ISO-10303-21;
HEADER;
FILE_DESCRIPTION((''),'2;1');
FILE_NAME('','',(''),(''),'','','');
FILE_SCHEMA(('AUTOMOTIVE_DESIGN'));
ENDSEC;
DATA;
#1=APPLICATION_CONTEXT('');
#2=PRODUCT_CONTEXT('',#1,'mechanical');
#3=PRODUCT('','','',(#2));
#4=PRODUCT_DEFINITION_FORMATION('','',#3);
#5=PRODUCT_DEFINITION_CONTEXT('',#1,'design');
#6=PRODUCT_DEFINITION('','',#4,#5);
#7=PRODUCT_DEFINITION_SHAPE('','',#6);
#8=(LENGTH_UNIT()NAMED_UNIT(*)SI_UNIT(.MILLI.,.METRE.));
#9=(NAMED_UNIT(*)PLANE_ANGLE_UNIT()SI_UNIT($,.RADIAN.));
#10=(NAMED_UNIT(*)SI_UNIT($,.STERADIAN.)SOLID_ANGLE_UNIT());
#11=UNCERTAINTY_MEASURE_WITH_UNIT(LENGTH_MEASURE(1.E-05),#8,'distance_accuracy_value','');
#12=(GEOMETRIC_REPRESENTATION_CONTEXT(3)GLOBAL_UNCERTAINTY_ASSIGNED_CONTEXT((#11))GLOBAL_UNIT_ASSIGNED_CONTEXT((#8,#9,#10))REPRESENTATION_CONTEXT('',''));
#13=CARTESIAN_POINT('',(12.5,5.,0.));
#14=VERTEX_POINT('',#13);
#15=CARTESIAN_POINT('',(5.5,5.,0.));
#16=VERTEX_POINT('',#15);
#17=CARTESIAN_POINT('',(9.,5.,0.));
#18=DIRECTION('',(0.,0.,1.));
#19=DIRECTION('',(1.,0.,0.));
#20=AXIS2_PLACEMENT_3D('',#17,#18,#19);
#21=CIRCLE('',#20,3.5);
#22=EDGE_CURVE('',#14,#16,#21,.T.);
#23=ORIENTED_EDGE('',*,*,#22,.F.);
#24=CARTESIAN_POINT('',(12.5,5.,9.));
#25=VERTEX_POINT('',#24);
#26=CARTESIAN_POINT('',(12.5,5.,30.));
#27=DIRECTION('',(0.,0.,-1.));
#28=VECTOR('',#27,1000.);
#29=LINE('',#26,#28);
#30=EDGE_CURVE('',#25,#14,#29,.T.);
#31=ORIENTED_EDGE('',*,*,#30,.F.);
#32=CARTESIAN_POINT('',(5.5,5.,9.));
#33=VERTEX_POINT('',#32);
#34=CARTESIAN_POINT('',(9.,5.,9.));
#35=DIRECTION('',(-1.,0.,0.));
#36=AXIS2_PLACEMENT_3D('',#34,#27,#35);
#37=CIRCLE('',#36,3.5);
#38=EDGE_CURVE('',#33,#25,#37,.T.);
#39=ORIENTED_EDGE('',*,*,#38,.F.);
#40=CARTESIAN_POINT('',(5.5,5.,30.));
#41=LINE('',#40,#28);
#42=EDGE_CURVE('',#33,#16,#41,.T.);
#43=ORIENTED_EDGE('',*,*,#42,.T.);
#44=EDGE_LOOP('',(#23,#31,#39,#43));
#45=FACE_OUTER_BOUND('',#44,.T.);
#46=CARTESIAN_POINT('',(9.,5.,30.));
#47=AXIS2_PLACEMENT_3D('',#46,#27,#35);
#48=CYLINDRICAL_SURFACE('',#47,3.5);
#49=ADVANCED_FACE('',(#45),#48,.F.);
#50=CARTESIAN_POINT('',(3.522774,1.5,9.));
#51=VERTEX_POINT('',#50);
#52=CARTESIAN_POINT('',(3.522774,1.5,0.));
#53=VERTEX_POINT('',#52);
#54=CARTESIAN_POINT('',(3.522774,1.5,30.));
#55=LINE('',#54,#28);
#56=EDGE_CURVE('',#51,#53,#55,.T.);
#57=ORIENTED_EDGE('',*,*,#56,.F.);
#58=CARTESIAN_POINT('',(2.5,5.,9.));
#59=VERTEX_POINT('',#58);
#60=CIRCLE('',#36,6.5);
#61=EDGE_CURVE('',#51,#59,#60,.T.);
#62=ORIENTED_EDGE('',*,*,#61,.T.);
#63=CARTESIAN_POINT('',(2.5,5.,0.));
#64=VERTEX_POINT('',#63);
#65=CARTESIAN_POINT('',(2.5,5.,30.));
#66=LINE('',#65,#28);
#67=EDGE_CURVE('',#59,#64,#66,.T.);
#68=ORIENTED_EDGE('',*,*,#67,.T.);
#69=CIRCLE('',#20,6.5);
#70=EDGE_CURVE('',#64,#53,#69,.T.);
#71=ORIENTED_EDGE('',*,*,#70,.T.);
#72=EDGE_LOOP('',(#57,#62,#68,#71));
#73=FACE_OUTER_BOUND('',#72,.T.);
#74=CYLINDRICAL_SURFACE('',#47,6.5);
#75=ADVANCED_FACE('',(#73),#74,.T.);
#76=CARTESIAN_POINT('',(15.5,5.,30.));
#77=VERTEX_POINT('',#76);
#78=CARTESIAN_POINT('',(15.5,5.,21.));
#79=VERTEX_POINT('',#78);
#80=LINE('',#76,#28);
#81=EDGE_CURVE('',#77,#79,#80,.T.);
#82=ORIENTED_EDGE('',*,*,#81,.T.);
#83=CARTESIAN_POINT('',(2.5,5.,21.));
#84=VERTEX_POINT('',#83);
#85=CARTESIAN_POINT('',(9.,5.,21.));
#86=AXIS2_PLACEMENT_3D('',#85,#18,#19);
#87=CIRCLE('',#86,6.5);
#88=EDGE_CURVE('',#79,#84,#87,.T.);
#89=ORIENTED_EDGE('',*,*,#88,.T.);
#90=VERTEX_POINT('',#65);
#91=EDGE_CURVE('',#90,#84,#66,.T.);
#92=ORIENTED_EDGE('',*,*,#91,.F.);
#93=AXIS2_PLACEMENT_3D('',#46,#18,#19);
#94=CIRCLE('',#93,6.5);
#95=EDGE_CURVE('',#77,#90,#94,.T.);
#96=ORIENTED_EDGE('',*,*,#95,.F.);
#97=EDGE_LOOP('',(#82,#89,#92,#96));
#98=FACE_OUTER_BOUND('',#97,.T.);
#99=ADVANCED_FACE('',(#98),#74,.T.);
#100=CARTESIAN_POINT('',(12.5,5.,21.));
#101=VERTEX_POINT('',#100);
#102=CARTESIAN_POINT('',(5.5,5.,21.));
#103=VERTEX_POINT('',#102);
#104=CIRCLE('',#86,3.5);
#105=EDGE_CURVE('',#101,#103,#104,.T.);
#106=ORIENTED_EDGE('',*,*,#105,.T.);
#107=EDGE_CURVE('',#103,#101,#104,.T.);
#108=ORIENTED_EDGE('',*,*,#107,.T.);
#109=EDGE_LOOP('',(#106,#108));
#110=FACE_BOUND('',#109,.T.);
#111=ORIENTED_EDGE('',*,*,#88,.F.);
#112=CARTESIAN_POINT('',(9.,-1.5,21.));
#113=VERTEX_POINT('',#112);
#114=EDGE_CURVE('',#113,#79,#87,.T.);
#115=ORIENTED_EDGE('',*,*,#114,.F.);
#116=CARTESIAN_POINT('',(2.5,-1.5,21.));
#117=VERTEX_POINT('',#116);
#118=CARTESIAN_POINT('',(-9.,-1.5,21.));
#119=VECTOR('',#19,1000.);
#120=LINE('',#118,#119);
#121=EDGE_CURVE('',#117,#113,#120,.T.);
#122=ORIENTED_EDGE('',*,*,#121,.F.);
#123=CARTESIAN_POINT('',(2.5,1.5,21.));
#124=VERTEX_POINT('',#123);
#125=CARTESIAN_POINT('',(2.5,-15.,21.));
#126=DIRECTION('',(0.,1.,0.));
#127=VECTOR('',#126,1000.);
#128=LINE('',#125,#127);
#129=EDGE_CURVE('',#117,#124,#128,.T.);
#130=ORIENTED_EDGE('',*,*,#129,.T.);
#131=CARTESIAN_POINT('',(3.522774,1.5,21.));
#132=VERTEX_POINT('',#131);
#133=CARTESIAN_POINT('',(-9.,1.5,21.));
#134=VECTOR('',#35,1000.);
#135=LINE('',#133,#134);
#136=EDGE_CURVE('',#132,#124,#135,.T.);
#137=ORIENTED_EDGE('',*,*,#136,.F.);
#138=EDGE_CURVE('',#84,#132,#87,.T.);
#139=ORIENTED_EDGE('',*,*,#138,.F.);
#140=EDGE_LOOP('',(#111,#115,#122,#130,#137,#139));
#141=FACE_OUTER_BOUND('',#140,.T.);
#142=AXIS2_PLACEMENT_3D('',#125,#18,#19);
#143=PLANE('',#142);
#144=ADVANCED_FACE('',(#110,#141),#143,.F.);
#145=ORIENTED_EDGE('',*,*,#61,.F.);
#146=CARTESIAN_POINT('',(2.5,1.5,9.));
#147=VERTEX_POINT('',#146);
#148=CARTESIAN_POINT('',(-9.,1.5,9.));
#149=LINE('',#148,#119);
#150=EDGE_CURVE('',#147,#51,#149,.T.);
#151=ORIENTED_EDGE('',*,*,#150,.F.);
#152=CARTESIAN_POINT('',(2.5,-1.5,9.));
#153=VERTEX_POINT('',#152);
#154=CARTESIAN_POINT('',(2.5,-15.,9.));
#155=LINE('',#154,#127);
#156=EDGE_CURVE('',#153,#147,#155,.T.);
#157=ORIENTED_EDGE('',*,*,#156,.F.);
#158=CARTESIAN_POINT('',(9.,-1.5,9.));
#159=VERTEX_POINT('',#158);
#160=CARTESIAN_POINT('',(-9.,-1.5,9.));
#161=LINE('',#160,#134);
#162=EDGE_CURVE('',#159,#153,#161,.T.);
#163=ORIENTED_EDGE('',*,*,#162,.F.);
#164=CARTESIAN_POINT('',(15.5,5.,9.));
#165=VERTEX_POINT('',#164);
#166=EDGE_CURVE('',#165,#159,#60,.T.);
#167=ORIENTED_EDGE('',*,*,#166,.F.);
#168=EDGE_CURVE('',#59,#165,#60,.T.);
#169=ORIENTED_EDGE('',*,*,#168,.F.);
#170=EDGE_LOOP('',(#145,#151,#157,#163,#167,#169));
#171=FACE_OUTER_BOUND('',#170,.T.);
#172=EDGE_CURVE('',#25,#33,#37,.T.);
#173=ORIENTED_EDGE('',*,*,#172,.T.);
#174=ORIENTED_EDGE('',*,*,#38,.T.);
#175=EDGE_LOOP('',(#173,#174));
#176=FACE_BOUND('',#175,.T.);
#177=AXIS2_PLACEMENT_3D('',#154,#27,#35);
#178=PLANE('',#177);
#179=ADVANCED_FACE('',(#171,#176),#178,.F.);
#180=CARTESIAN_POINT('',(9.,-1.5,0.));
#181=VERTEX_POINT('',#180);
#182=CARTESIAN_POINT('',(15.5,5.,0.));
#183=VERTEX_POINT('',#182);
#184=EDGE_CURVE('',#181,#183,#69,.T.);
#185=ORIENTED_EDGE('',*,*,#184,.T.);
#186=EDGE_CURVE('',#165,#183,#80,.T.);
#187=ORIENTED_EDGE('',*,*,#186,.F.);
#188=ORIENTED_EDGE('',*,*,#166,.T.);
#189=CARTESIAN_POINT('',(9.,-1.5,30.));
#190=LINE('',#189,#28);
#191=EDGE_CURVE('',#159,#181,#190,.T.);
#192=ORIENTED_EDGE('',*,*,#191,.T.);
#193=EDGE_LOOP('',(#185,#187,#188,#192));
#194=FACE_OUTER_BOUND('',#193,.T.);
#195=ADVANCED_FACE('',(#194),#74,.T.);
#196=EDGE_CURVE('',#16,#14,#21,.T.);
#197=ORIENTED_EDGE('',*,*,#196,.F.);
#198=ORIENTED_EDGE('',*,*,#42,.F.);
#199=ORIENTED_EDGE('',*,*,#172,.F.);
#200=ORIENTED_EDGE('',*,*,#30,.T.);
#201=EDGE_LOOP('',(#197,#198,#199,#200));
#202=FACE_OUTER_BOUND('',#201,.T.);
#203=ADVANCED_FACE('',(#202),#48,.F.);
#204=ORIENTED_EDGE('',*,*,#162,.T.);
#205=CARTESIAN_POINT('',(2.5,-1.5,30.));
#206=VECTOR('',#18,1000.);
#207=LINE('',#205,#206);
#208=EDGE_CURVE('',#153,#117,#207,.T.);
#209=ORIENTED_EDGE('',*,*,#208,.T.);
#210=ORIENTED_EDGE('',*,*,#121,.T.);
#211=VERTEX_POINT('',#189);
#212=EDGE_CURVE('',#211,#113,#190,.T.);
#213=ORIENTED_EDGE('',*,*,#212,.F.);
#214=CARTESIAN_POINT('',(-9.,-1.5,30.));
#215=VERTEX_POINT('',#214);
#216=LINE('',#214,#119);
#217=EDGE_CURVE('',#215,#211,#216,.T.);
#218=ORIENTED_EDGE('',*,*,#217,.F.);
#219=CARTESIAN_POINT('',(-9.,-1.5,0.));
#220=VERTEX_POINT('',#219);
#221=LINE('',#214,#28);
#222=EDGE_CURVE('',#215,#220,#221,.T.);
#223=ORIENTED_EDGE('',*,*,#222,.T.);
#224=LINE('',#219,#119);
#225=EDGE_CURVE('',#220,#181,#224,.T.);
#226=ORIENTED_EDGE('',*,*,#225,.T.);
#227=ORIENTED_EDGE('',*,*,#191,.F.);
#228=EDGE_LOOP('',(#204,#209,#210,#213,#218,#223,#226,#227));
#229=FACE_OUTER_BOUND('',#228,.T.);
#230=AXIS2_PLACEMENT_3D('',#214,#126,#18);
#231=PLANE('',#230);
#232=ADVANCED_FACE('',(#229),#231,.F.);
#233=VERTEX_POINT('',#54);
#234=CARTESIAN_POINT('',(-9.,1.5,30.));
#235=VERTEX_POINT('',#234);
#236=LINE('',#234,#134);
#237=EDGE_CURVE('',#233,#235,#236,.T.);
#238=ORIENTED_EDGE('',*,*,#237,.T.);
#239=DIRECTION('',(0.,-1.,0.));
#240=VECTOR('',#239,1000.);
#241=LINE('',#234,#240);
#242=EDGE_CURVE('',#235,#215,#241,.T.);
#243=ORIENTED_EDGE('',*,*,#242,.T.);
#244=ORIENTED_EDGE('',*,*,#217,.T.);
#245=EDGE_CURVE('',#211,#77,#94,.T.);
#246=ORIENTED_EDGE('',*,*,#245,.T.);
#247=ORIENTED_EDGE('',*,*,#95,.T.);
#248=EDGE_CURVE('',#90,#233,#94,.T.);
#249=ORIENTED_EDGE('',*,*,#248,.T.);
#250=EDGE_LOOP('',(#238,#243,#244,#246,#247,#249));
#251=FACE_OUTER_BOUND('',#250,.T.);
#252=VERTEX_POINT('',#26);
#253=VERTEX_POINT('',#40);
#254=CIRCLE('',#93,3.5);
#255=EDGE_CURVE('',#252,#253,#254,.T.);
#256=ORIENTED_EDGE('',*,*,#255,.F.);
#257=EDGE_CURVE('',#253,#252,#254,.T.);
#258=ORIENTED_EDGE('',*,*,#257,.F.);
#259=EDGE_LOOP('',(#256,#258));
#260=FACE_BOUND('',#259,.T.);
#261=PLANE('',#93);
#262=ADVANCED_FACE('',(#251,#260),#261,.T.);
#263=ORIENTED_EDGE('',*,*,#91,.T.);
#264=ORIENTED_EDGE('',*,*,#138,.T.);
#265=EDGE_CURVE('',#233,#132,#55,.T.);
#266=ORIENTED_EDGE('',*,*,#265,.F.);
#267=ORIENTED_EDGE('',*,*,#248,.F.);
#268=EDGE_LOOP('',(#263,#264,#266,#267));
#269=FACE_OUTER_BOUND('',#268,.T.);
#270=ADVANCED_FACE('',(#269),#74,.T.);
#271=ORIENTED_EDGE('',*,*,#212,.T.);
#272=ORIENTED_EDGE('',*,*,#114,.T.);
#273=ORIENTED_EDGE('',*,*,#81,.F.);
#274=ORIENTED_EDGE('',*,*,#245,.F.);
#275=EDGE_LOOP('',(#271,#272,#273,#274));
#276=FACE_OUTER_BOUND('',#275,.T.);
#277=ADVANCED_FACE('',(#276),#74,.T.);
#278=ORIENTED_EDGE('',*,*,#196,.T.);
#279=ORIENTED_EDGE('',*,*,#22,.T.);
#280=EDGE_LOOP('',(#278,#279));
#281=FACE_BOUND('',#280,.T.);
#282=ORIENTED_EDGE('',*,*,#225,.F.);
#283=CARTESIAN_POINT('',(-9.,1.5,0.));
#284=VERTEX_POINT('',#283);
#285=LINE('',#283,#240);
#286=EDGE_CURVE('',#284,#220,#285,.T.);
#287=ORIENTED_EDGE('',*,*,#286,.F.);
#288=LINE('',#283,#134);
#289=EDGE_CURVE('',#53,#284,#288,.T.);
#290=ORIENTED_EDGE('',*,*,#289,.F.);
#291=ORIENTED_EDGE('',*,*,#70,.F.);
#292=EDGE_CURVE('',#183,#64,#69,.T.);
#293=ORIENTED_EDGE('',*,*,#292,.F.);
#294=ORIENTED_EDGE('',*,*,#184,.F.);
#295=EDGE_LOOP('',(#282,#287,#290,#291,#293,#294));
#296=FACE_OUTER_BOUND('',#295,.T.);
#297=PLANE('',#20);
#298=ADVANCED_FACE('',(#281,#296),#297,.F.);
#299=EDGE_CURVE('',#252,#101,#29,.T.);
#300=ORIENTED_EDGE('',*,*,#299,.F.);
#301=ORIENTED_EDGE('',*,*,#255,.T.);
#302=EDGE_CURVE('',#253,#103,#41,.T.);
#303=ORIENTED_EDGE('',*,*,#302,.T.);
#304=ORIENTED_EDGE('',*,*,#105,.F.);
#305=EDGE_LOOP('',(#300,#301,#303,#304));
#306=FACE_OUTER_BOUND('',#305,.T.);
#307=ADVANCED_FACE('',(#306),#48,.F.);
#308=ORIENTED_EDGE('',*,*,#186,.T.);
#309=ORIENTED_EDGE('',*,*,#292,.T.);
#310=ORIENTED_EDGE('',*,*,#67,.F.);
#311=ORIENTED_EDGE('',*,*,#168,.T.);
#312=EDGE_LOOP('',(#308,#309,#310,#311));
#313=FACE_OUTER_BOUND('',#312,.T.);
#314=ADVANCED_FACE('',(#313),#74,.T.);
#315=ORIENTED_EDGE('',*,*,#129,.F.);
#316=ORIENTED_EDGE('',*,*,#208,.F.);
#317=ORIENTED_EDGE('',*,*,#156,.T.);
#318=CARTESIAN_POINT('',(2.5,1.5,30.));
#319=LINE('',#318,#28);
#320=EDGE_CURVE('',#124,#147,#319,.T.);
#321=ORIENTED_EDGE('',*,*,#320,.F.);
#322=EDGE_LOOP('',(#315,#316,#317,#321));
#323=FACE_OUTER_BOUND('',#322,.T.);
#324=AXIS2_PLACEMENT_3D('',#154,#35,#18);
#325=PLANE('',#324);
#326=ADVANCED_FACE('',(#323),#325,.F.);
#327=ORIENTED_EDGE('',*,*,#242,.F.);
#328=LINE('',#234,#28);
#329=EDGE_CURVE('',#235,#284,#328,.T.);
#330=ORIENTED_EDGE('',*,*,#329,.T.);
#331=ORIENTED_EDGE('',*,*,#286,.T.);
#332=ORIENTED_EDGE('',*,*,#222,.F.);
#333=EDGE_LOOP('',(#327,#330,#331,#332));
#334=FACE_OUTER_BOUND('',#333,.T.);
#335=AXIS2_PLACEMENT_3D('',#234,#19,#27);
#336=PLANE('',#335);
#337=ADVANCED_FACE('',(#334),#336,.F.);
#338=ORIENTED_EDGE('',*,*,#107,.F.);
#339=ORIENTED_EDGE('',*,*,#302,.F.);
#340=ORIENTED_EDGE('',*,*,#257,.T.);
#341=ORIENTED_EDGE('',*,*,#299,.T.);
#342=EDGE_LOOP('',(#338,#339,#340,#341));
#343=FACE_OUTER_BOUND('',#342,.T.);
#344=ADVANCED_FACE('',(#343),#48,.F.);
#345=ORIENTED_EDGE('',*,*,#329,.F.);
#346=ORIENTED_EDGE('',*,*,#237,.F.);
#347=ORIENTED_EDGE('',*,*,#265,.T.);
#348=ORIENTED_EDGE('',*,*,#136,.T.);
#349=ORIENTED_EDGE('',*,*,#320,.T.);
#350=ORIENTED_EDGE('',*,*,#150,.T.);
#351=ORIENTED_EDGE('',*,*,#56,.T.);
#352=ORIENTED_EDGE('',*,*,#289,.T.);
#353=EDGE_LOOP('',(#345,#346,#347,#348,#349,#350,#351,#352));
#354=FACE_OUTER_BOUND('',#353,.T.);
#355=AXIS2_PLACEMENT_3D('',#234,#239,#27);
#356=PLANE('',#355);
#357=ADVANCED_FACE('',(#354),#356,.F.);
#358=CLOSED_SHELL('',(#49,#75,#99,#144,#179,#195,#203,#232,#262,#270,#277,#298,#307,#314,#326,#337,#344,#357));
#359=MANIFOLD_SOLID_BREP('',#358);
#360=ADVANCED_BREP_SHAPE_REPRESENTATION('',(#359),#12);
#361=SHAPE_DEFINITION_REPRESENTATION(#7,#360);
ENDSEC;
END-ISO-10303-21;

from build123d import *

# Parameters (mm, degrees)
SKETCH_1_R          = 3.5
EXTRUDE_1_DEPTH     = 30
SKETCH_2_W          = 19.333042973
SKETCH_2_H          = 12
CUT_EXTRUDE_1_DEPTH = 15


with BuildPart() as part:
    # 草图1 → 凸台-拉伸1 (new body)
    with BuildSketch(Plane.XY):
        with BuildLine():
            Line((-9, 1.5), (3.522774425, 1.5))
            ThreePointArc((3.522774425, 1.5), (12.122498999, 10.700877125), (9, -1.5))
            Line((9, -1.5), (-9, -1.5))
            Line((-9, -1.5), (-9, 1.5))
        make_face()
        with Locations((9, 5)):
            Circle(SKETCH_1_R, mode=Mode.SUBTRACT)
    extrude(amount=EXTRUDE_1_DEPTH)

    # 草图2 → 切除-拉伸1 (cut, symmetric)
    with BuildSketch(Plane(origin=(0, 0, 0), x_dir=(1, 0, 0), z_dir=(0, 1, 0))):
        with Locations((12.166521487, -15)):
            Rectangle(SKETCH_2_W, SKETCH_2_H)
    extrude(amount=CUT_EXTRUDE_1_DEPTH, both=True, mode=Mode.SUBTRACT)


solid = part.part
